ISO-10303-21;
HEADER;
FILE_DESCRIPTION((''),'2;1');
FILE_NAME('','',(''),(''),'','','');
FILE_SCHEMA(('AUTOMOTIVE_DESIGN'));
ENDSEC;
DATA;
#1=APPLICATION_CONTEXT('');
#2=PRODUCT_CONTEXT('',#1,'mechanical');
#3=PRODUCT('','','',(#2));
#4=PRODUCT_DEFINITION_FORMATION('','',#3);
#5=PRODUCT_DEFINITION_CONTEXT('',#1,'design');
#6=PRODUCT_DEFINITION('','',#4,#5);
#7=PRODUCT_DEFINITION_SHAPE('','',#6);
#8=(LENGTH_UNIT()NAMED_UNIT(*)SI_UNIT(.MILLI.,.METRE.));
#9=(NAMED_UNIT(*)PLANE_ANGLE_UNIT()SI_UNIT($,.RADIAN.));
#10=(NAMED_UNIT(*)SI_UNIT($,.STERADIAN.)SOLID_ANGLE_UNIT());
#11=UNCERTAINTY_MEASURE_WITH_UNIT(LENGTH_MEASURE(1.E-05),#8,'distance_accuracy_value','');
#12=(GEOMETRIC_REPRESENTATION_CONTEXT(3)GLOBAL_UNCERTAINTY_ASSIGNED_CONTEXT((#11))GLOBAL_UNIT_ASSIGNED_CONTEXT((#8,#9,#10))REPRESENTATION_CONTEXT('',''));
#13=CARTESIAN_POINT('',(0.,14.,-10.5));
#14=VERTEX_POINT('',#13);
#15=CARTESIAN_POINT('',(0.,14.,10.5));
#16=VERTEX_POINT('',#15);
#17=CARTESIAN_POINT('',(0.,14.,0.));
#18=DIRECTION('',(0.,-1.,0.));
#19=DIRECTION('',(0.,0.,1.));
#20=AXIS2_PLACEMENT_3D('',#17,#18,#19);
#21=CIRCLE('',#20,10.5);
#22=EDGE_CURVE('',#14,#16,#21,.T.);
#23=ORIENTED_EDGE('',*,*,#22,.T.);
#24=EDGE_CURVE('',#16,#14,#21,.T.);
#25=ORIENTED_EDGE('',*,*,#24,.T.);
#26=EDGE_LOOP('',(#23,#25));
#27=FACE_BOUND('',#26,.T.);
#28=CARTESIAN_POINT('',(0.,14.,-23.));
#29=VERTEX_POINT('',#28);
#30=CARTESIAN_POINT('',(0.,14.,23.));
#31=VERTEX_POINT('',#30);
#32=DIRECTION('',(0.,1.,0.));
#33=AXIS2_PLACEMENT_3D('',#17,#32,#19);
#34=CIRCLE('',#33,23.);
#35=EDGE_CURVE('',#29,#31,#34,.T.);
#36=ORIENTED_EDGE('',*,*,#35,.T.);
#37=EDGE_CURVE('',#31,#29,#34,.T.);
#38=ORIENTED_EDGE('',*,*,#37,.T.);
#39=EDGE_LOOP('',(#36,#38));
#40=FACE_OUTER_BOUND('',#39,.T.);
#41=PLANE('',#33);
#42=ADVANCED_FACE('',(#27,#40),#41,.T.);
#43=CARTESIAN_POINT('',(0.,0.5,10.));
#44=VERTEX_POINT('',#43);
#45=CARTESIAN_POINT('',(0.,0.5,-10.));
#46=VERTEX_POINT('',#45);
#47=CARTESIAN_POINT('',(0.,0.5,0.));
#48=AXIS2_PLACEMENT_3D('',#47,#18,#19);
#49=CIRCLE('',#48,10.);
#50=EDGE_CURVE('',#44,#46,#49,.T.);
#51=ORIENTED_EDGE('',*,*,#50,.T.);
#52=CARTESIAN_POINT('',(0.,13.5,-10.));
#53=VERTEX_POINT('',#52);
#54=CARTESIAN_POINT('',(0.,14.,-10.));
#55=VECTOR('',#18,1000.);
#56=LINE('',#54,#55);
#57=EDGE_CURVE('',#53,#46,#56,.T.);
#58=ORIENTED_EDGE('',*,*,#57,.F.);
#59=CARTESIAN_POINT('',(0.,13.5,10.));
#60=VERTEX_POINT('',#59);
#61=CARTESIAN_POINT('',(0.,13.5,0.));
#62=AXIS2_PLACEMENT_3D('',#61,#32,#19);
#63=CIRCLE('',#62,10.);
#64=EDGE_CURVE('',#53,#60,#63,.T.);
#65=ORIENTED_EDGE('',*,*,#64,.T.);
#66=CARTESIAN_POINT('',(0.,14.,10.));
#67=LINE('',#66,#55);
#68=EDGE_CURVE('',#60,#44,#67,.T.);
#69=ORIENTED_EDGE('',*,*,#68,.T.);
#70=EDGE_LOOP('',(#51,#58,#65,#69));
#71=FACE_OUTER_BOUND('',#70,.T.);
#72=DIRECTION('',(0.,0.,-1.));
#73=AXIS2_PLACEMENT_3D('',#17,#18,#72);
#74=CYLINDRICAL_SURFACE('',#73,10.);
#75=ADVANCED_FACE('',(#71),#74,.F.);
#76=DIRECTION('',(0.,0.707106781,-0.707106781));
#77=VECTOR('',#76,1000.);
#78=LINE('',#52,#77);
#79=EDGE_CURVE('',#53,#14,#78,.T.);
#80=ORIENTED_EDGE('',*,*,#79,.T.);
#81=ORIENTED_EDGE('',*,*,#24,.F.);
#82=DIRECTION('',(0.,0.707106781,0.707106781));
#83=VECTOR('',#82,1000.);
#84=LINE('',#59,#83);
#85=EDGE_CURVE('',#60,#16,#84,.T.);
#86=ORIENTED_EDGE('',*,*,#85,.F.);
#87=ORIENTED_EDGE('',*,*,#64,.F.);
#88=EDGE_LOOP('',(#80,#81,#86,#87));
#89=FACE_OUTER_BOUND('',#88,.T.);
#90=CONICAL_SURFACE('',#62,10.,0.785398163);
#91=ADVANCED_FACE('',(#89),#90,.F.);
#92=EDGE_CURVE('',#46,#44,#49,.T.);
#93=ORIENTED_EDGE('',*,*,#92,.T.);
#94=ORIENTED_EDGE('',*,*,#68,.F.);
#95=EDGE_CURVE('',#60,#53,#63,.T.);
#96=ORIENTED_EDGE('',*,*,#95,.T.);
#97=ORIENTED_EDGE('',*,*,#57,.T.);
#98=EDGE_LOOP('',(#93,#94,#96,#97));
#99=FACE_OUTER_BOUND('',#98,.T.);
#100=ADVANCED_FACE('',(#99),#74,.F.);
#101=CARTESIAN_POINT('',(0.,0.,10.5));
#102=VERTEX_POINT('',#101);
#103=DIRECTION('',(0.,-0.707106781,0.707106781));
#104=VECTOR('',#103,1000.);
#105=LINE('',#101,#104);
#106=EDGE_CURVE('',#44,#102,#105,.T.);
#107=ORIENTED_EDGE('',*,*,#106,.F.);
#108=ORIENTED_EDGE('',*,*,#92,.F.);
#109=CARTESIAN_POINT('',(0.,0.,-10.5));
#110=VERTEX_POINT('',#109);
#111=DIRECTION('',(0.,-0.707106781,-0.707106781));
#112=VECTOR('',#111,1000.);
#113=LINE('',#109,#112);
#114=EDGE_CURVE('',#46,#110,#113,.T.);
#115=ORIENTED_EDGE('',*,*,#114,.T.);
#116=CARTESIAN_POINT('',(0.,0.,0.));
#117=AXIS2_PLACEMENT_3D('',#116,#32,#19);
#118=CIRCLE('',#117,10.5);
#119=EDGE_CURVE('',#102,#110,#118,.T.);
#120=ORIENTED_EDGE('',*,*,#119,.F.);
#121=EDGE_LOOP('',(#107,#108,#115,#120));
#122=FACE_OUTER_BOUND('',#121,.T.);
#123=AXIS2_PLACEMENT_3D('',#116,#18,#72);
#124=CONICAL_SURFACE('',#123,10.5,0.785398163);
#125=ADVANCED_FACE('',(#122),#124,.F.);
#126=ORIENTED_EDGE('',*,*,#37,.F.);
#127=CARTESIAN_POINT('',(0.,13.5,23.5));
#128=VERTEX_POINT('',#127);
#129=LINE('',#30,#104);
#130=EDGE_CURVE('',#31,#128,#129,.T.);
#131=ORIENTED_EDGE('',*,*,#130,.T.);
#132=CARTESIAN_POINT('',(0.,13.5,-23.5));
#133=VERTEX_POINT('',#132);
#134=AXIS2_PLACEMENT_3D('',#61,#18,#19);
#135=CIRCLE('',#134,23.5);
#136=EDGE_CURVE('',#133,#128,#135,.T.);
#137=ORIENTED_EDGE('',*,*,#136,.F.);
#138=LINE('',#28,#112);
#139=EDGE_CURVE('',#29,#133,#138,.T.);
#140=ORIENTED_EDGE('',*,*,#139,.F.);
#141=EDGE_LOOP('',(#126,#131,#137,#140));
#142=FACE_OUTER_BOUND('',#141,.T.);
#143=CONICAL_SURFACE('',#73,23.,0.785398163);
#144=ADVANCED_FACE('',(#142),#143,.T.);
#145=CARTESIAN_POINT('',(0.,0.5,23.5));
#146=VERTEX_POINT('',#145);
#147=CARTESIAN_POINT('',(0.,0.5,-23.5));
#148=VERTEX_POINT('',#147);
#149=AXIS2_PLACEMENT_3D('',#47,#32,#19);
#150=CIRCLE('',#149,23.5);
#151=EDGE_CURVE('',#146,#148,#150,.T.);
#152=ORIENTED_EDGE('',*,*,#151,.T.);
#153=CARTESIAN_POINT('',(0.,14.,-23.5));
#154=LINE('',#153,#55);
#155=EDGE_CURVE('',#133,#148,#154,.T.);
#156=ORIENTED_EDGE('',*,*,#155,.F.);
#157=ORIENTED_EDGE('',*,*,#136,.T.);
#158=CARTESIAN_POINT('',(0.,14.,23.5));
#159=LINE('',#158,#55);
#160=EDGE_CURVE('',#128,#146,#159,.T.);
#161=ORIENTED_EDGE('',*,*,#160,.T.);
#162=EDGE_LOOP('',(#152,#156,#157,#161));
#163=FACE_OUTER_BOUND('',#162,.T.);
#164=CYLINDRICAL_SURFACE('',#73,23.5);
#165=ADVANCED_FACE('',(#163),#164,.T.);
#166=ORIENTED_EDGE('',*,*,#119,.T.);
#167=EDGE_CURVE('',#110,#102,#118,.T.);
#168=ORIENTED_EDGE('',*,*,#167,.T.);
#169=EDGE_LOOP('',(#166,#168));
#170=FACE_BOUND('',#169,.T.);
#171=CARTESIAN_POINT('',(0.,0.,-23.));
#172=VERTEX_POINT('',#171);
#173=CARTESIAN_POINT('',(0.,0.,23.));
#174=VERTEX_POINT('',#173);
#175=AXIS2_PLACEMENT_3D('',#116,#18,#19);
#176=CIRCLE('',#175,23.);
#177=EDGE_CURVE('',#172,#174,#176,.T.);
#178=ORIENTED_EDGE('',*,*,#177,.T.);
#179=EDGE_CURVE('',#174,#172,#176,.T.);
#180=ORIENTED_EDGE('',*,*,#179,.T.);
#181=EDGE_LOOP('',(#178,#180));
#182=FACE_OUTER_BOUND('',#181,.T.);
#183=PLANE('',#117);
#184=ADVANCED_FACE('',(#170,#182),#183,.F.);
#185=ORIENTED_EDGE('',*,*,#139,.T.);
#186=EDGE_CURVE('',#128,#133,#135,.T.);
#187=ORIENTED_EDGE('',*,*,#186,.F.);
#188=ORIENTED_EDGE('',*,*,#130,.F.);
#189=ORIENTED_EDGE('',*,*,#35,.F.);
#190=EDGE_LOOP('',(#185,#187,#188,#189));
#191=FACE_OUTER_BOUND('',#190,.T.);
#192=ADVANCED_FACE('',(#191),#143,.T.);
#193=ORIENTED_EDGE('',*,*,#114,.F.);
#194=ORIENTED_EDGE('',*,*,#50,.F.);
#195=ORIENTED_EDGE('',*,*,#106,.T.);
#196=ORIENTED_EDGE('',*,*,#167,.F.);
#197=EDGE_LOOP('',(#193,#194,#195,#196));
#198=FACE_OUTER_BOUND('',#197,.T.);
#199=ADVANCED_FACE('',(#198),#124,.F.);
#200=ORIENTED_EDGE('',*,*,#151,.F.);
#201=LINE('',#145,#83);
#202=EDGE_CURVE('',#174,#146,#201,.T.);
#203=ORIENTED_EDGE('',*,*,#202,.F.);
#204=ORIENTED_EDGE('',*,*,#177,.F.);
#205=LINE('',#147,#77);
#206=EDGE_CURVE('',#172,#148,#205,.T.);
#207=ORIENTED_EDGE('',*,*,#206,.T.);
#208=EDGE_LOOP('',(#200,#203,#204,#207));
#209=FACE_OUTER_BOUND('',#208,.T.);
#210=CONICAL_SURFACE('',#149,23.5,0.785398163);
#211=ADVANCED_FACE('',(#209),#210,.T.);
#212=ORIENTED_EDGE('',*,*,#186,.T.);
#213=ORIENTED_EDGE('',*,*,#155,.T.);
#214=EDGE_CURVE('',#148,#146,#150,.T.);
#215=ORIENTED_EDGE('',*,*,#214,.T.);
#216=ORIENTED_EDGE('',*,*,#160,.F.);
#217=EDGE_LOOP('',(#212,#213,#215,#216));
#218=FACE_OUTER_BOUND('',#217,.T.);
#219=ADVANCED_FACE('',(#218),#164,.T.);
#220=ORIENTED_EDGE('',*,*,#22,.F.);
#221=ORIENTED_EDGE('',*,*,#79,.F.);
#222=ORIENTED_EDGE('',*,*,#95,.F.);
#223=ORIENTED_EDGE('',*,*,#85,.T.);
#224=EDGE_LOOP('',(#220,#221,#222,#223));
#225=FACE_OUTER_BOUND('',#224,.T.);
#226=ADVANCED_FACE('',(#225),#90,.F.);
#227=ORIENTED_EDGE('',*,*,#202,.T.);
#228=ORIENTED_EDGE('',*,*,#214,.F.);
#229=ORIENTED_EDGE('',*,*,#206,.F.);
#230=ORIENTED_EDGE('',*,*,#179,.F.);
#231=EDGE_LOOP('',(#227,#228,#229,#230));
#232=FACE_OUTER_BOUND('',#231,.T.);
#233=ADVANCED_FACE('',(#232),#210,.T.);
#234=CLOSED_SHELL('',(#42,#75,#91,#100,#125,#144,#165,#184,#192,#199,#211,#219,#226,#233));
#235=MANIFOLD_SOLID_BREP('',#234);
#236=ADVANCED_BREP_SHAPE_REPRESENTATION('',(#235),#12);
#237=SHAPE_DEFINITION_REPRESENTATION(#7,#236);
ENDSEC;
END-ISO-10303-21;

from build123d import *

# Parameters (mm, degrees)
SKETCH_1_R      = 23.5
SKETCH_1_R_2    = 10
EXTRUDE_1_DEPTH = 14
CHAMFER_1_SIZE  = 0.5


with BuildPart() as part:
    # 草图1 → 拉伸1 (new body)
    with BuildSketch(Plane(origin=(0, 0, 0), x_dir=(1, 0, 0), z_dir=(0, 1, 0))):
        with Locations(Location((0, 0, 0), (0, 0, 270))):
            Circle(SKETCH_1_R)
        with Locations(Location((0, 0, 0), (0, 0, 270))):
            Circle(SKETCH_1_R_2, mode=Mode.SUBTRACT)
    extrude(amount=EXTRUDE_1_DEPTH)

    # 倒角1
    chamfer_1_edges = [part.edges().sort_by_distance(p)[0] for p in [
        (0, 0, -23.5),
        (0, 14, -23.5),
        (0, 0, -10),
        (0, 14, -10),
    ]]
    chamfer(chamfer_1_edges, length=CHAMFER_1_SIZE)


solid = part.part
